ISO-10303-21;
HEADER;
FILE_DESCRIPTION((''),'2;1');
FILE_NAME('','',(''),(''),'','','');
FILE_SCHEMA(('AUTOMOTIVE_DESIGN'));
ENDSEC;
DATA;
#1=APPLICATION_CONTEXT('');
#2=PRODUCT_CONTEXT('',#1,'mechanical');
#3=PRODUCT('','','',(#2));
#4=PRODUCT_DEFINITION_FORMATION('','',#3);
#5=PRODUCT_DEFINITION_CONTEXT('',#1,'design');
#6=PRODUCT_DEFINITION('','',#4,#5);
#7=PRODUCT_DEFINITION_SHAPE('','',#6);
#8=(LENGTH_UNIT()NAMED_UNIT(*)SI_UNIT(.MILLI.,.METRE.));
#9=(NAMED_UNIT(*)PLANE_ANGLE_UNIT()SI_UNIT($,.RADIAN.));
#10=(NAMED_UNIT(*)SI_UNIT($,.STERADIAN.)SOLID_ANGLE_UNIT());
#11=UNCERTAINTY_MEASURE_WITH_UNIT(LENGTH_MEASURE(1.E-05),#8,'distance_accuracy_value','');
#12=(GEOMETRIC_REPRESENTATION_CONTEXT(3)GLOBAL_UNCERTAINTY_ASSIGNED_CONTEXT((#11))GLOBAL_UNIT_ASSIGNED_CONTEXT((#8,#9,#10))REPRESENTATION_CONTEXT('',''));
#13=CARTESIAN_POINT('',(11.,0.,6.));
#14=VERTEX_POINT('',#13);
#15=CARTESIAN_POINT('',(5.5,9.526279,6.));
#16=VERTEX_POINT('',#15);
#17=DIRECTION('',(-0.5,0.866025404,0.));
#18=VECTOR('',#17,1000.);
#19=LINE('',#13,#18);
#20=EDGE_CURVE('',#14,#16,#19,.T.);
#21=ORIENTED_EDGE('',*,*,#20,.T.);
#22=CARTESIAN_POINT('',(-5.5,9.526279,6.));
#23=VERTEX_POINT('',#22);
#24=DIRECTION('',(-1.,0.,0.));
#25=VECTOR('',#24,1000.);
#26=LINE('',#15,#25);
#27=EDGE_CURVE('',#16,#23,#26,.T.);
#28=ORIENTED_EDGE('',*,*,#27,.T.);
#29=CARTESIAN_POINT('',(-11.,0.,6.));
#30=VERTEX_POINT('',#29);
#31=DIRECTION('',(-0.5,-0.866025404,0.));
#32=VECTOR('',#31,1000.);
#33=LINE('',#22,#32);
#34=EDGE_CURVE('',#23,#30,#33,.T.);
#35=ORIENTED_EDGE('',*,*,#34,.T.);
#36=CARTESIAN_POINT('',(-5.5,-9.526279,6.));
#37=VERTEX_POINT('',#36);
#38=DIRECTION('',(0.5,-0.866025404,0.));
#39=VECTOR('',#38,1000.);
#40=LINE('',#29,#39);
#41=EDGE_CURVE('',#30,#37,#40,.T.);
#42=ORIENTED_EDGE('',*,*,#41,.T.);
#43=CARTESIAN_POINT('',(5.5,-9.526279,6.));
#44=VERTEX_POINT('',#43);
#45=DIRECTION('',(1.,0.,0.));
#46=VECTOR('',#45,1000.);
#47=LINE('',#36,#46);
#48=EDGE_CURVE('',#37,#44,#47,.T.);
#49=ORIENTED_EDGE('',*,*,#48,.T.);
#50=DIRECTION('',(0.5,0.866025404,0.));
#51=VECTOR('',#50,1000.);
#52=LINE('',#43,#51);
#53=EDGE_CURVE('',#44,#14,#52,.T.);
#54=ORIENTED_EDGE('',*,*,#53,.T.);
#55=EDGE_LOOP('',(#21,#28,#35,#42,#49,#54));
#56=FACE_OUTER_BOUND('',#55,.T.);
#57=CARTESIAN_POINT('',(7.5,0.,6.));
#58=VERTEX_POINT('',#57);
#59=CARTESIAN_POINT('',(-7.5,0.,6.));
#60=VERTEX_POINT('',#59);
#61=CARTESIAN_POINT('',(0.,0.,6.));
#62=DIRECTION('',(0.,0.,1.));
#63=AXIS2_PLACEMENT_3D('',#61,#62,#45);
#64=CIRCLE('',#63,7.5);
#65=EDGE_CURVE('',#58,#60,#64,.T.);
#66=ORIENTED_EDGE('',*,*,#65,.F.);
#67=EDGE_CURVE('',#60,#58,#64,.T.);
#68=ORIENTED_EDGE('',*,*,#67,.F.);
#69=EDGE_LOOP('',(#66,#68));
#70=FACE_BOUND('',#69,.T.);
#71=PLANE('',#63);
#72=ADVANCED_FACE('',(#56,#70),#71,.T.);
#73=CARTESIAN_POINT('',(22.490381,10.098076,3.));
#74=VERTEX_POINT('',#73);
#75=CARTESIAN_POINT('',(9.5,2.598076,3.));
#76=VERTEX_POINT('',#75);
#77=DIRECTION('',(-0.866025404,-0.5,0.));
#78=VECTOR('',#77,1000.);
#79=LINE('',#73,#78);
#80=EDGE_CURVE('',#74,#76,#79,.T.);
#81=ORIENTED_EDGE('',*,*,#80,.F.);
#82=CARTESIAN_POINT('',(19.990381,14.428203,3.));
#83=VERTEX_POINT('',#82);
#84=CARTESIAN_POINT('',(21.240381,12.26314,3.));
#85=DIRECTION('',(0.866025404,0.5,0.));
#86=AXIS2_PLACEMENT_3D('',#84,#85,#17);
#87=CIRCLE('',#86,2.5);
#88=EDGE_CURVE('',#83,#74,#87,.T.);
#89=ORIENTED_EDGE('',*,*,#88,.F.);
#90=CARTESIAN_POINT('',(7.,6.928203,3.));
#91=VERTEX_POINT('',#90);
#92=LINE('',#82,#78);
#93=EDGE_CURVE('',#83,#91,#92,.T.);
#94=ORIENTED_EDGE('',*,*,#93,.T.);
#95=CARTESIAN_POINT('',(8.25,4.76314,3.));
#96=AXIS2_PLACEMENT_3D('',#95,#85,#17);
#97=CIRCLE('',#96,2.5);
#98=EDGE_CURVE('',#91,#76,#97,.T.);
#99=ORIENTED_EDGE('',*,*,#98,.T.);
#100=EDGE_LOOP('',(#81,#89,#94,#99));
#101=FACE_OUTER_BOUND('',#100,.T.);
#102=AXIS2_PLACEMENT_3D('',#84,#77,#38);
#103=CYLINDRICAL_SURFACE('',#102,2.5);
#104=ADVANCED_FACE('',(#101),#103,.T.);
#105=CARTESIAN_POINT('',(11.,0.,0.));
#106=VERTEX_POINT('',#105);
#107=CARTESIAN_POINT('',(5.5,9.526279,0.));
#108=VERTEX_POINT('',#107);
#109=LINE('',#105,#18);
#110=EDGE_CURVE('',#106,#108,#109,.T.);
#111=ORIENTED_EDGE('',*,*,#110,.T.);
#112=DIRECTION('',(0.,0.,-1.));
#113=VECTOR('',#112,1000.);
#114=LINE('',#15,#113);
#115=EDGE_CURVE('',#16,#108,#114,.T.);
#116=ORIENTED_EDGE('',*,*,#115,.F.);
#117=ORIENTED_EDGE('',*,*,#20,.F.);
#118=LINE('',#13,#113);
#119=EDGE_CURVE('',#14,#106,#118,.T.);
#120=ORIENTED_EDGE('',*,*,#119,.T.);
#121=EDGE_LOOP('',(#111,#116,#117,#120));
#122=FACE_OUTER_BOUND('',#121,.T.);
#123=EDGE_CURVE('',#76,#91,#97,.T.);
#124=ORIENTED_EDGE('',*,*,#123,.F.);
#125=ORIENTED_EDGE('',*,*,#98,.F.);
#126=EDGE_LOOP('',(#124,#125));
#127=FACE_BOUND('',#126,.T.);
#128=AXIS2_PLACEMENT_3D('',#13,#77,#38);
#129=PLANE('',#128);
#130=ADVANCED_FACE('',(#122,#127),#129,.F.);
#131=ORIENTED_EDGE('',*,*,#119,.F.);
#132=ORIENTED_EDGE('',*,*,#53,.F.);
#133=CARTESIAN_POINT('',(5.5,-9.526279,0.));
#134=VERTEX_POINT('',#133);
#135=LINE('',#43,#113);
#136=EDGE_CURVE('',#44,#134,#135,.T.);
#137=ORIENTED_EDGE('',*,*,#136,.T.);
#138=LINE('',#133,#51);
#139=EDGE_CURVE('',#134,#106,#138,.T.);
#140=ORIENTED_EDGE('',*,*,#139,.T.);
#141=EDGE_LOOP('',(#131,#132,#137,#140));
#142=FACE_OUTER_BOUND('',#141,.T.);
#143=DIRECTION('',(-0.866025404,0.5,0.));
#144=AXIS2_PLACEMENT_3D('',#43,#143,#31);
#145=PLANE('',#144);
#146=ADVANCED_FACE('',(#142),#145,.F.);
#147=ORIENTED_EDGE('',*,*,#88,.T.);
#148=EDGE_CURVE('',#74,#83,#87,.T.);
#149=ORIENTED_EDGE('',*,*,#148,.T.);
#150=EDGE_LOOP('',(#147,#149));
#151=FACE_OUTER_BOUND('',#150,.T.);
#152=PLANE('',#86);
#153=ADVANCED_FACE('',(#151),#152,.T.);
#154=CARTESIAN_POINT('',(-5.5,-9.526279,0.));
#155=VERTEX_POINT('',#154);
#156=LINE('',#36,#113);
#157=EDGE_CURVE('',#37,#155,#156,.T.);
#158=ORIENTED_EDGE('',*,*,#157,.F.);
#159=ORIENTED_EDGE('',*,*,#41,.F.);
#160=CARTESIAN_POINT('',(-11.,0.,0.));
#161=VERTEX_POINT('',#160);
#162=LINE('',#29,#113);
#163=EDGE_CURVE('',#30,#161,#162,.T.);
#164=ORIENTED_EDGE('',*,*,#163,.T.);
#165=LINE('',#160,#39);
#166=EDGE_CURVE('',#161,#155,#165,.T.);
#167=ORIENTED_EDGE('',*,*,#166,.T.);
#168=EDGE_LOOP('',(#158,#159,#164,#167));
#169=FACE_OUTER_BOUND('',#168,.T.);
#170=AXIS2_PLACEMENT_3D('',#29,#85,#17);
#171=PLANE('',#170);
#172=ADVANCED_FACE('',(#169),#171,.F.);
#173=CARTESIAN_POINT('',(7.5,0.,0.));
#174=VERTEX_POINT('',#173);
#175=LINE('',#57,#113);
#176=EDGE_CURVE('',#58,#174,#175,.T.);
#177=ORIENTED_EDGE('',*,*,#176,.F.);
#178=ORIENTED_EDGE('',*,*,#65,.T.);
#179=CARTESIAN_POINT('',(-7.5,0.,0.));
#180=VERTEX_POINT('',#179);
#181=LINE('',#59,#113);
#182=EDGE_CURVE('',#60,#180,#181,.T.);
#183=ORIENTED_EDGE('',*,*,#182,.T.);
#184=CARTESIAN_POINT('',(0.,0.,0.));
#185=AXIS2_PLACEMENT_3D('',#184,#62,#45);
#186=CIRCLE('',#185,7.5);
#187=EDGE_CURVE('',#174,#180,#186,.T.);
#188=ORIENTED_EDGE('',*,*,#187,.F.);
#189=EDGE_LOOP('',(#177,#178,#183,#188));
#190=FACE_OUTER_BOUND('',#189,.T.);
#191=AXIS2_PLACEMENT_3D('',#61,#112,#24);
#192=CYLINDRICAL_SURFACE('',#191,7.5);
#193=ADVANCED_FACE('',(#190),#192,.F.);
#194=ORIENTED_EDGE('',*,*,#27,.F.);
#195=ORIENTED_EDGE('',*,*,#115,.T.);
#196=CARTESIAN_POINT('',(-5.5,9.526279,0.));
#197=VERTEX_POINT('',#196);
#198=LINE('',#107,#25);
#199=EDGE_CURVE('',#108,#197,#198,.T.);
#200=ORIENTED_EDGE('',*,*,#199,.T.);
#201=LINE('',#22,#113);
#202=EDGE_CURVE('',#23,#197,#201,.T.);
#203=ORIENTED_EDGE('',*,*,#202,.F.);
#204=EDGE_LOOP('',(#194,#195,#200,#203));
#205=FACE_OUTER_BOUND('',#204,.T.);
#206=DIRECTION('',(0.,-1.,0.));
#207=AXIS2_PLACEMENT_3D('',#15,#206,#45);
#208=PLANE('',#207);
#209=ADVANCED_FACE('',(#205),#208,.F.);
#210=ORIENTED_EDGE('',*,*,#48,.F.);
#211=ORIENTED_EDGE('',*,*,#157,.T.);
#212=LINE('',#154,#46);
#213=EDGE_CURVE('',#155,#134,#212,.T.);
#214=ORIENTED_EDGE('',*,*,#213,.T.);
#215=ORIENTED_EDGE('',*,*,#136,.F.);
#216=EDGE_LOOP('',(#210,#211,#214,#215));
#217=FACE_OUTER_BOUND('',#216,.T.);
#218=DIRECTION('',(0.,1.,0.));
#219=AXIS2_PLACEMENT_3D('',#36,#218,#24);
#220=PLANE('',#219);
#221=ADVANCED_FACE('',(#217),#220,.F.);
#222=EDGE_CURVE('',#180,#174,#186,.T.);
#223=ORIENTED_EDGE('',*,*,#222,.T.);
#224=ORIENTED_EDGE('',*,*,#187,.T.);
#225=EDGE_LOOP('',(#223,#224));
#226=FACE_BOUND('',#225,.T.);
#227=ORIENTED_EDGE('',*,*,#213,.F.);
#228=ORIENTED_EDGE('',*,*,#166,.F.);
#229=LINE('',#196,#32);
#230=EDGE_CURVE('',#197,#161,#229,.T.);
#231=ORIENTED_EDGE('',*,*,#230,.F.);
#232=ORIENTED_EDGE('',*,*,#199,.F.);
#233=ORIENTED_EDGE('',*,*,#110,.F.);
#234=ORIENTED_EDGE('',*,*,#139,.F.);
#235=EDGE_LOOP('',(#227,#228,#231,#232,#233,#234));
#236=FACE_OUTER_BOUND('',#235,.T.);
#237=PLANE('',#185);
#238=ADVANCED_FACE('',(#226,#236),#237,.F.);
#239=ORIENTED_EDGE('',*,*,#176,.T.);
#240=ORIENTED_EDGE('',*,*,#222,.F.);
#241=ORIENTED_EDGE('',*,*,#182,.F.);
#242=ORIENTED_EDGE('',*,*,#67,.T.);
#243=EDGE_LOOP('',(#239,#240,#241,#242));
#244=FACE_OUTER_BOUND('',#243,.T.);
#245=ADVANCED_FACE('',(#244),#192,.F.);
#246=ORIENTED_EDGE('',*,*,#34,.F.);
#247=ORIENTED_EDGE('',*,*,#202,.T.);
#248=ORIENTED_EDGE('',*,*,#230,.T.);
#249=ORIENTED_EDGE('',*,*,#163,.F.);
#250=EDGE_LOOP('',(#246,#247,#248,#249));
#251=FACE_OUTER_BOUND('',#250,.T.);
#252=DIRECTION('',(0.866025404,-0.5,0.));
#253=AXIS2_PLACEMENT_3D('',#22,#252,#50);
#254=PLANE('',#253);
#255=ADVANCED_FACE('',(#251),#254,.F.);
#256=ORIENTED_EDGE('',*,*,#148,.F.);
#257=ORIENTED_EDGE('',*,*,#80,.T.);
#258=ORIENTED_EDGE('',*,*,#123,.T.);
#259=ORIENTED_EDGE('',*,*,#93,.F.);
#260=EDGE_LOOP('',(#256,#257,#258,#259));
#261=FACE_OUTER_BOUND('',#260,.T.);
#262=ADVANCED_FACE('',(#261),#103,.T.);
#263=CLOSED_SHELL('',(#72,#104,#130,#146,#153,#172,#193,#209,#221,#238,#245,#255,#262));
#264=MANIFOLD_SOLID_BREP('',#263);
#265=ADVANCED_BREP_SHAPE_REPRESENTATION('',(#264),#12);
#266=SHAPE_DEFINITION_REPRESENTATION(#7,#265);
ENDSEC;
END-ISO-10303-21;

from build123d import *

# Parameters (mm, degrees)
SKETCH1_R           = 7.5
BOSS_EXTRUDE1_DEPTH = 6
SKETCH2_R           = 2.5
BOSS_EXTRUDE2_DEPTH = 15


with BuildPart() as part:
    # Sketch1 → Boss-Extrude1 (new body)
    with BuildSketch(Plane.XY):
        Polygon((-5.5, 9.526279442), (-11, 0), (-5.5, -9.526279442), (5.5, -9.526279442), (11, 0), (5.5, 9.526279442), align=None)
        Circle(SKETCH1_R, mode=Mode.SUBTRACT)
    extrude(amount=BOSS_EXTRUDE1_DEPTH)

    # Sketch2 → Boss-Extrude2 (add)
    with BuildSketch(Plane(origin=(8.25, 4.763139721, 0), x_dir=(0, 0, -1), z_dir=(0.8660254037844389, 0.49999999999999983, 0))):
        with Locations(Location((-3, 0, 0), (0, 0, 90))):
            Circle(SKETCH2_R)
    extrude(amount=BOSS_EXTRUDE2_DEPTH)


solid = part.part
